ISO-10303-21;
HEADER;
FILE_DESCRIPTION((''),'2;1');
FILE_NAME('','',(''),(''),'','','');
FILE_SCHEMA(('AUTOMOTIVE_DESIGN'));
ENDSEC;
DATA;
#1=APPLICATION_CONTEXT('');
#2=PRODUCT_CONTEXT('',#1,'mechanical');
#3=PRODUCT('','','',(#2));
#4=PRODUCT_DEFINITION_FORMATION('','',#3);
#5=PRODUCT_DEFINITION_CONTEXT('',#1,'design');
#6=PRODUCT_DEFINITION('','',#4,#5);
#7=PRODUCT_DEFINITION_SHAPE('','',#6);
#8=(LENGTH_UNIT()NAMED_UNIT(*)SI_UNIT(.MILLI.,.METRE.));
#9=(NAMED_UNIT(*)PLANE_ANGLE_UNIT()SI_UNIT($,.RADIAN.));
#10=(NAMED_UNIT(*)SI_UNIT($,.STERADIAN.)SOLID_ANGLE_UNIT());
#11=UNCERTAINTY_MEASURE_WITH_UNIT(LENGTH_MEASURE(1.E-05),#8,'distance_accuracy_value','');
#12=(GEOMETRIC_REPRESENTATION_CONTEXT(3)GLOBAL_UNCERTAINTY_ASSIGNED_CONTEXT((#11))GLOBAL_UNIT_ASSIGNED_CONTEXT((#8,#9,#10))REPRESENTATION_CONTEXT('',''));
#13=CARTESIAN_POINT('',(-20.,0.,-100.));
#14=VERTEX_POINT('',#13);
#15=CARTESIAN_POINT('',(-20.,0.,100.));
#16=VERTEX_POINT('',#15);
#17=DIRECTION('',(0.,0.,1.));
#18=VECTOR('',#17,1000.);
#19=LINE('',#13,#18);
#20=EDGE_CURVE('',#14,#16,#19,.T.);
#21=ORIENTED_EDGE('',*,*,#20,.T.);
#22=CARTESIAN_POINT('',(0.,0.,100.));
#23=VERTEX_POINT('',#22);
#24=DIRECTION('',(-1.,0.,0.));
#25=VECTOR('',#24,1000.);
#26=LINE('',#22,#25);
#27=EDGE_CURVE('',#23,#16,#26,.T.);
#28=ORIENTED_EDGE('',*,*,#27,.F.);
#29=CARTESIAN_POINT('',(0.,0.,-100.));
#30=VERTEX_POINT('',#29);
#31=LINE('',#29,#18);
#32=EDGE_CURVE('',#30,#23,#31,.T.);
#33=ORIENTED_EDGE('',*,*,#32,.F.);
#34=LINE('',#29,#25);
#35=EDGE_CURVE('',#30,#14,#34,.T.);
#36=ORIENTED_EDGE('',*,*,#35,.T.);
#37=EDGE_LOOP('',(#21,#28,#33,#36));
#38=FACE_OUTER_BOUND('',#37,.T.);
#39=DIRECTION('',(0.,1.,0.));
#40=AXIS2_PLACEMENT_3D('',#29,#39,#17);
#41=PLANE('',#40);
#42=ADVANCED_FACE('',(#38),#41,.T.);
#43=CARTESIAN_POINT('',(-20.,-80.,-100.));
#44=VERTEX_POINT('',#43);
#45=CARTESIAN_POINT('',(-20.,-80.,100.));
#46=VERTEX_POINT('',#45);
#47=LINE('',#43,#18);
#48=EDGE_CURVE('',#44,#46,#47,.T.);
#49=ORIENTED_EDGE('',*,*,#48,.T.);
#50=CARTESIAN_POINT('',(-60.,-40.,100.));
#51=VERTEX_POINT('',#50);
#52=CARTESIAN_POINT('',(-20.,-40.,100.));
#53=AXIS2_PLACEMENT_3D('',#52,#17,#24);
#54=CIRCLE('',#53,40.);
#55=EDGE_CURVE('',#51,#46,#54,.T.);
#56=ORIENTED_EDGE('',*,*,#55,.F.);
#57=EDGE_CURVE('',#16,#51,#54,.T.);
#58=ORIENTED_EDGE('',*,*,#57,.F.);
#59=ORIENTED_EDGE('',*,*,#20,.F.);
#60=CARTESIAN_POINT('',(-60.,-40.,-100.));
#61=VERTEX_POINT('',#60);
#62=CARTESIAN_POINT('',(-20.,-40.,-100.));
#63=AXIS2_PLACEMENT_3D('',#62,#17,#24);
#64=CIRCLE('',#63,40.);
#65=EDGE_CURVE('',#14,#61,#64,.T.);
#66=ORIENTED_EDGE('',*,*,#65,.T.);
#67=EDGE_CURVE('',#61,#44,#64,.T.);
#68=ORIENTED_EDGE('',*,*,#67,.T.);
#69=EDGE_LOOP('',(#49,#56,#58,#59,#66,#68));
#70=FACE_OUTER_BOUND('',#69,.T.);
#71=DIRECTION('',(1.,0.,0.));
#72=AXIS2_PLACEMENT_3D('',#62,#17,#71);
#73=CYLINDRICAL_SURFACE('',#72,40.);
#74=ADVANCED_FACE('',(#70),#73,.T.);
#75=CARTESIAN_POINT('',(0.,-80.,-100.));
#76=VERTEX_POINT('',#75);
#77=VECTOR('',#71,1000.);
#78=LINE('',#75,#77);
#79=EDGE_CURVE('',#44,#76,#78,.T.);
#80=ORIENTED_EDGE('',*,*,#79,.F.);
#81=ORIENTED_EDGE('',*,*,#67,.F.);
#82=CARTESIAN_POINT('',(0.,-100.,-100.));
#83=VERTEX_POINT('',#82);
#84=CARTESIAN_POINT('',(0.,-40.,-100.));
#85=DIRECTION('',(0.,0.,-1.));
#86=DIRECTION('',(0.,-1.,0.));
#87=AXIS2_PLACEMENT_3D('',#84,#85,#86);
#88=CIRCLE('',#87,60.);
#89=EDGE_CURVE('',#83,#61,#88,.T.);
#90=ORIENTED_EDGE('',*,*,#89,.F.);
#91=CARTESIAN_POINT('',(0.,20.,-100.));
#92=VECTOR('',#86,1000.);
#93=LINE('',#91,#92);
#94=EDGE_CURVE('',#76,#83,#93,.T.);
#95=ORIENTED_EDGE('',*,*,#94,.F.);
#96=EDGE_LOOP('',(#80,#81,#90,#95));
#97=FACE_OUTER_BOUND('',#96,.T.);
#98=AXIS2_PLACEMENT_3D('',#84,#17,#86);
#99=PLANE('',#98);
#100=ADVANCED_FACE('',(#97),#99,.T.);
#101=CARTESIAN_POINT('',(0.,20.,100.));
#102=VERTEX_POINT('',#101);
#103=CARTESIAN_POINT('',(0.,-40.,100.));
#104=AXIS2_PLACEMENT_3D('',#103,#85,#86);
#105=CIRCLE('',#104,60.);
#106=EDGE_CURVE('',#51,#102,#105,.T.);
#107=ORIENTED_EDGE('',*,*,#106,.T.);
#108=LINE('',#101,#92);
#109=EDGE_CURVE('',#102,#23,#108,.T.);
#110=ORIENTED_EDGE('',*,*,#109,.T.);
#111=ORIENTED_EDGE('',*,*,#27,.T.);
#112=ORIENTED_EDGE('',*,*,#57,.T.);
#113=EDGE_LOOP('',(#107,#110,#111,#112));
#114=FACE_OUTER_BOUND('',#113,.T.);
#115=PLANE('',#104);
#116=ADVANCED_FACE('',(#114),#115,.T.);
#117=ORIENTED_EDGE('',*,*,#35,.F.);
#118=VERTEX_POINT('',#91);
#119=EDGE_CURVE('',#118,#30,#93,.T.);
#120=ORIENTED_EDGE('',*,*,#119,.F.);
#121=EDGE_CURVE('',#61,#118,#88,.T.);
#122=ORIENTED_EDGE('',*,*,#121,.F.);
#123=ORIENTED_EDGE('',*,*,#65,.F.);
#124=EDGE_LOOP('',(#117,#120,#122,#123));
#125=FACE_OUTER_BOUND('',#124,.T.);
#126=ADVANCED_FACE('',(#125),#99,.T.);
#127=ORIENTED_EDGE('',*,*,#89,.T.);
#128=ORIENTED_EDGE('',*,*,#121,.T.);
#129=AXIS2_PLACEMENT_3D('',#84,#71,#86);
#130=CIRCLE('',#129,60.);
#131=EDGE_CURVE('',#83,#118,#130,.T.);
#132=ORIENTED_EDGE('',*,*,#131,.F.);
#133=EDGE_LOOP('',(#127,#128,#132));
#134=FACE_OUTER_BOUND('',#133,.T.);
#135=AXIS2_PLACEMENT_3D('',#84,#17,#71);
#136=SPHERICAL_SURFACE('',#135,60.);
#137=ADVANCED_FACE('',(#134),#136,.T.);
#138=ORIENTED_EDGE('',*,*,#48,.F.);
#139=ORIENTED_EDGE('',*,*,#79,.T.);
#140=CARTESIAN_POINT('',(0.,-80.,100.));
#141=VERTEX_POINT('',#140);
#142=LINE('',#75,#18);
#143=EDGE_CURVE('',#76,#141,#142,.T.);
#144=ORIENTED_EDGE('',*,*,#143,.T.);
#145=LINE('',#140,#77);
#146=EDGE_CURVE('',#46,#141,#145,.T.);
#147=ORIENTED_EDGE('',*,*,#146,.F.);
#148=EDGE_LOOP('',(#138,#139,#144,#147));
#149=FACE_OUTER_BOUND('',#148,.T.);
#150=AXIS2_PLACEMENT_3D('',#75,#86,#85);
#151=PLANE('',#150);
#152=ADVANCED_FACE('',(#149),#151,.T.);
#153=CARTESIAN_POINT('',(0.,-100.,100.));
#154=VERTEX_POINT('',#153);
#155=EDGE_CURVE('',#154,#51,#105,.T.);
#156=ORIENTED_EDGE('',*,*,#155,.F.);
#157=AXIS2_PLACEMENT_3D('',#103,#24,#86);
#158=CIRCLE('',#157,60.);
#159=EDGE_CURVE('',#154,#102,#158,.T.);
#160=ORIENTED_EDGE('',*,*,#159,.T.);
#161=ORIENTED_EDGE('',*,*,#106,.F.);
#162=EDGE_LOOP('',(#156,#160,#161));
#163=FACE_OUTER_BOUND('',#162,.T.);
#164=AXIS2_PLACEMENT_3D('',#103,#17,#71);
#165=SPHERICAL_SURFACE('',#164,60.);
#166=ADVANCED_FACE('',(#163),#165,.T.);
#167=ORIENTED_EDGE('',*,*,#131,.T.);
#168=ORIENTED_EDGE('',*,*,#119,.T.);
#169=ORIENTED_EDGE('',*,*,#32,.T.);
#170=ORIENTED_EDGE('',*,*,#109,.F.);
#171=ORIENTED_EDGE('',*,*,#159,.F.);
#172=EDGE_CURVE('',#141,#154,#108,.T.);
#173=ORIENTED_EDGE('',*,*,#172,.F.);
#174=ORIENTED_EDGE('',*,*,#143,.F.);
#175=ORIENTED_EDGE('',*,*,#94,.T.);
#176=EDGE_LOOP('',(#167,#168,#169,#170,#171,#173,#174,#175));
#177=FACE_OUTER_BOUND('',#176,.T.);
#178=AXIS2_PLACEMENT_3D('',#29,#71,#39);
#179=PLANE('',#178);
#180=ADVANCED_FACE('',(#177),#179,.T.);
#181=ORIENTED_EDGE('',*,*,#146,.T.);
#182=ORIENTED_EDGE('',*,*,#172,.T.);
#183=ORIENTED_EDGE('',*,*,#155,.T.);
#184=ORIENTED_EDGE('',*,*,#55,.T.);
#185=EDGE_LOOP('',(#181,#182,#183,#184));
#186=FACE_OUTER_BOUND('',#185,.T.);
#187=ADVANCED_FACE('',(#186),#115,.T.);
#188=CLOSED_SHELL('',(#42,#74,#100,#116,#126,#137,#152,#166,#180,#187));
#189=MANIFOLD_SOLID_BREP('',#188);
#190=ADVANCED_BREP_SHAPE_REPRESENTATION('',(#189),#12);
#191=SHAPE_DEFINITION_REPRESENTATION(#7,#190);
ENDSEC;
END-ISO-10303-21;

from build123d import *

# Parameters (mm, degrees)
EXTRUDE_1_DEPTH = 100
REVOLVE_1_ANGLE = 90


with BuildPart() as part:
    # 草图1 → 凸台-拉伸1 (new body)
    with BuildSketch(Plane.XY):
        with BuildLine():
            Line((0, 0), (0, -80))
            Line((0, -80), (-20, -80))
            ThreePointArc((-20, -80), (-60, -40), (-20, 0))
            Line((-20, 0), (0, 0))
        make_face()
    extrude_1 = extrude(amount=-EXTRUDE_1_DEPTH)

    # 草图2 → 旋转1 (revolve)
    with BuildSketch(Plane(origin=(0, 0, 0), x_dir=(0, 0, -1), z_dir=(1, 0, 0))):
        with BuildLine():
            Line((100, 20), (100, -100))
            ThreePointArc((100, -100), (160, -40), (100, 20))
        make_face()
    revolve_1 = revolve(axis=Axis((0, 20, -100), (0, 1, 0)), revolution_arc=REVOLVE_1_ANGLE)

    # 镜向1: 凸台-拉伸1, 旋转1 across plane
    add(extrude_1.mirror(Plane(origin=(-20, -40, 0), x_dir=(1, 0, 0), z_dir=(0, 0, -1))))
    add(revolve_1.mirror(Plane(origin=(-20, -40, 0), x_dir=(1, 0, 0), z_dir=(0, 0, -1))))


solid = part.part
